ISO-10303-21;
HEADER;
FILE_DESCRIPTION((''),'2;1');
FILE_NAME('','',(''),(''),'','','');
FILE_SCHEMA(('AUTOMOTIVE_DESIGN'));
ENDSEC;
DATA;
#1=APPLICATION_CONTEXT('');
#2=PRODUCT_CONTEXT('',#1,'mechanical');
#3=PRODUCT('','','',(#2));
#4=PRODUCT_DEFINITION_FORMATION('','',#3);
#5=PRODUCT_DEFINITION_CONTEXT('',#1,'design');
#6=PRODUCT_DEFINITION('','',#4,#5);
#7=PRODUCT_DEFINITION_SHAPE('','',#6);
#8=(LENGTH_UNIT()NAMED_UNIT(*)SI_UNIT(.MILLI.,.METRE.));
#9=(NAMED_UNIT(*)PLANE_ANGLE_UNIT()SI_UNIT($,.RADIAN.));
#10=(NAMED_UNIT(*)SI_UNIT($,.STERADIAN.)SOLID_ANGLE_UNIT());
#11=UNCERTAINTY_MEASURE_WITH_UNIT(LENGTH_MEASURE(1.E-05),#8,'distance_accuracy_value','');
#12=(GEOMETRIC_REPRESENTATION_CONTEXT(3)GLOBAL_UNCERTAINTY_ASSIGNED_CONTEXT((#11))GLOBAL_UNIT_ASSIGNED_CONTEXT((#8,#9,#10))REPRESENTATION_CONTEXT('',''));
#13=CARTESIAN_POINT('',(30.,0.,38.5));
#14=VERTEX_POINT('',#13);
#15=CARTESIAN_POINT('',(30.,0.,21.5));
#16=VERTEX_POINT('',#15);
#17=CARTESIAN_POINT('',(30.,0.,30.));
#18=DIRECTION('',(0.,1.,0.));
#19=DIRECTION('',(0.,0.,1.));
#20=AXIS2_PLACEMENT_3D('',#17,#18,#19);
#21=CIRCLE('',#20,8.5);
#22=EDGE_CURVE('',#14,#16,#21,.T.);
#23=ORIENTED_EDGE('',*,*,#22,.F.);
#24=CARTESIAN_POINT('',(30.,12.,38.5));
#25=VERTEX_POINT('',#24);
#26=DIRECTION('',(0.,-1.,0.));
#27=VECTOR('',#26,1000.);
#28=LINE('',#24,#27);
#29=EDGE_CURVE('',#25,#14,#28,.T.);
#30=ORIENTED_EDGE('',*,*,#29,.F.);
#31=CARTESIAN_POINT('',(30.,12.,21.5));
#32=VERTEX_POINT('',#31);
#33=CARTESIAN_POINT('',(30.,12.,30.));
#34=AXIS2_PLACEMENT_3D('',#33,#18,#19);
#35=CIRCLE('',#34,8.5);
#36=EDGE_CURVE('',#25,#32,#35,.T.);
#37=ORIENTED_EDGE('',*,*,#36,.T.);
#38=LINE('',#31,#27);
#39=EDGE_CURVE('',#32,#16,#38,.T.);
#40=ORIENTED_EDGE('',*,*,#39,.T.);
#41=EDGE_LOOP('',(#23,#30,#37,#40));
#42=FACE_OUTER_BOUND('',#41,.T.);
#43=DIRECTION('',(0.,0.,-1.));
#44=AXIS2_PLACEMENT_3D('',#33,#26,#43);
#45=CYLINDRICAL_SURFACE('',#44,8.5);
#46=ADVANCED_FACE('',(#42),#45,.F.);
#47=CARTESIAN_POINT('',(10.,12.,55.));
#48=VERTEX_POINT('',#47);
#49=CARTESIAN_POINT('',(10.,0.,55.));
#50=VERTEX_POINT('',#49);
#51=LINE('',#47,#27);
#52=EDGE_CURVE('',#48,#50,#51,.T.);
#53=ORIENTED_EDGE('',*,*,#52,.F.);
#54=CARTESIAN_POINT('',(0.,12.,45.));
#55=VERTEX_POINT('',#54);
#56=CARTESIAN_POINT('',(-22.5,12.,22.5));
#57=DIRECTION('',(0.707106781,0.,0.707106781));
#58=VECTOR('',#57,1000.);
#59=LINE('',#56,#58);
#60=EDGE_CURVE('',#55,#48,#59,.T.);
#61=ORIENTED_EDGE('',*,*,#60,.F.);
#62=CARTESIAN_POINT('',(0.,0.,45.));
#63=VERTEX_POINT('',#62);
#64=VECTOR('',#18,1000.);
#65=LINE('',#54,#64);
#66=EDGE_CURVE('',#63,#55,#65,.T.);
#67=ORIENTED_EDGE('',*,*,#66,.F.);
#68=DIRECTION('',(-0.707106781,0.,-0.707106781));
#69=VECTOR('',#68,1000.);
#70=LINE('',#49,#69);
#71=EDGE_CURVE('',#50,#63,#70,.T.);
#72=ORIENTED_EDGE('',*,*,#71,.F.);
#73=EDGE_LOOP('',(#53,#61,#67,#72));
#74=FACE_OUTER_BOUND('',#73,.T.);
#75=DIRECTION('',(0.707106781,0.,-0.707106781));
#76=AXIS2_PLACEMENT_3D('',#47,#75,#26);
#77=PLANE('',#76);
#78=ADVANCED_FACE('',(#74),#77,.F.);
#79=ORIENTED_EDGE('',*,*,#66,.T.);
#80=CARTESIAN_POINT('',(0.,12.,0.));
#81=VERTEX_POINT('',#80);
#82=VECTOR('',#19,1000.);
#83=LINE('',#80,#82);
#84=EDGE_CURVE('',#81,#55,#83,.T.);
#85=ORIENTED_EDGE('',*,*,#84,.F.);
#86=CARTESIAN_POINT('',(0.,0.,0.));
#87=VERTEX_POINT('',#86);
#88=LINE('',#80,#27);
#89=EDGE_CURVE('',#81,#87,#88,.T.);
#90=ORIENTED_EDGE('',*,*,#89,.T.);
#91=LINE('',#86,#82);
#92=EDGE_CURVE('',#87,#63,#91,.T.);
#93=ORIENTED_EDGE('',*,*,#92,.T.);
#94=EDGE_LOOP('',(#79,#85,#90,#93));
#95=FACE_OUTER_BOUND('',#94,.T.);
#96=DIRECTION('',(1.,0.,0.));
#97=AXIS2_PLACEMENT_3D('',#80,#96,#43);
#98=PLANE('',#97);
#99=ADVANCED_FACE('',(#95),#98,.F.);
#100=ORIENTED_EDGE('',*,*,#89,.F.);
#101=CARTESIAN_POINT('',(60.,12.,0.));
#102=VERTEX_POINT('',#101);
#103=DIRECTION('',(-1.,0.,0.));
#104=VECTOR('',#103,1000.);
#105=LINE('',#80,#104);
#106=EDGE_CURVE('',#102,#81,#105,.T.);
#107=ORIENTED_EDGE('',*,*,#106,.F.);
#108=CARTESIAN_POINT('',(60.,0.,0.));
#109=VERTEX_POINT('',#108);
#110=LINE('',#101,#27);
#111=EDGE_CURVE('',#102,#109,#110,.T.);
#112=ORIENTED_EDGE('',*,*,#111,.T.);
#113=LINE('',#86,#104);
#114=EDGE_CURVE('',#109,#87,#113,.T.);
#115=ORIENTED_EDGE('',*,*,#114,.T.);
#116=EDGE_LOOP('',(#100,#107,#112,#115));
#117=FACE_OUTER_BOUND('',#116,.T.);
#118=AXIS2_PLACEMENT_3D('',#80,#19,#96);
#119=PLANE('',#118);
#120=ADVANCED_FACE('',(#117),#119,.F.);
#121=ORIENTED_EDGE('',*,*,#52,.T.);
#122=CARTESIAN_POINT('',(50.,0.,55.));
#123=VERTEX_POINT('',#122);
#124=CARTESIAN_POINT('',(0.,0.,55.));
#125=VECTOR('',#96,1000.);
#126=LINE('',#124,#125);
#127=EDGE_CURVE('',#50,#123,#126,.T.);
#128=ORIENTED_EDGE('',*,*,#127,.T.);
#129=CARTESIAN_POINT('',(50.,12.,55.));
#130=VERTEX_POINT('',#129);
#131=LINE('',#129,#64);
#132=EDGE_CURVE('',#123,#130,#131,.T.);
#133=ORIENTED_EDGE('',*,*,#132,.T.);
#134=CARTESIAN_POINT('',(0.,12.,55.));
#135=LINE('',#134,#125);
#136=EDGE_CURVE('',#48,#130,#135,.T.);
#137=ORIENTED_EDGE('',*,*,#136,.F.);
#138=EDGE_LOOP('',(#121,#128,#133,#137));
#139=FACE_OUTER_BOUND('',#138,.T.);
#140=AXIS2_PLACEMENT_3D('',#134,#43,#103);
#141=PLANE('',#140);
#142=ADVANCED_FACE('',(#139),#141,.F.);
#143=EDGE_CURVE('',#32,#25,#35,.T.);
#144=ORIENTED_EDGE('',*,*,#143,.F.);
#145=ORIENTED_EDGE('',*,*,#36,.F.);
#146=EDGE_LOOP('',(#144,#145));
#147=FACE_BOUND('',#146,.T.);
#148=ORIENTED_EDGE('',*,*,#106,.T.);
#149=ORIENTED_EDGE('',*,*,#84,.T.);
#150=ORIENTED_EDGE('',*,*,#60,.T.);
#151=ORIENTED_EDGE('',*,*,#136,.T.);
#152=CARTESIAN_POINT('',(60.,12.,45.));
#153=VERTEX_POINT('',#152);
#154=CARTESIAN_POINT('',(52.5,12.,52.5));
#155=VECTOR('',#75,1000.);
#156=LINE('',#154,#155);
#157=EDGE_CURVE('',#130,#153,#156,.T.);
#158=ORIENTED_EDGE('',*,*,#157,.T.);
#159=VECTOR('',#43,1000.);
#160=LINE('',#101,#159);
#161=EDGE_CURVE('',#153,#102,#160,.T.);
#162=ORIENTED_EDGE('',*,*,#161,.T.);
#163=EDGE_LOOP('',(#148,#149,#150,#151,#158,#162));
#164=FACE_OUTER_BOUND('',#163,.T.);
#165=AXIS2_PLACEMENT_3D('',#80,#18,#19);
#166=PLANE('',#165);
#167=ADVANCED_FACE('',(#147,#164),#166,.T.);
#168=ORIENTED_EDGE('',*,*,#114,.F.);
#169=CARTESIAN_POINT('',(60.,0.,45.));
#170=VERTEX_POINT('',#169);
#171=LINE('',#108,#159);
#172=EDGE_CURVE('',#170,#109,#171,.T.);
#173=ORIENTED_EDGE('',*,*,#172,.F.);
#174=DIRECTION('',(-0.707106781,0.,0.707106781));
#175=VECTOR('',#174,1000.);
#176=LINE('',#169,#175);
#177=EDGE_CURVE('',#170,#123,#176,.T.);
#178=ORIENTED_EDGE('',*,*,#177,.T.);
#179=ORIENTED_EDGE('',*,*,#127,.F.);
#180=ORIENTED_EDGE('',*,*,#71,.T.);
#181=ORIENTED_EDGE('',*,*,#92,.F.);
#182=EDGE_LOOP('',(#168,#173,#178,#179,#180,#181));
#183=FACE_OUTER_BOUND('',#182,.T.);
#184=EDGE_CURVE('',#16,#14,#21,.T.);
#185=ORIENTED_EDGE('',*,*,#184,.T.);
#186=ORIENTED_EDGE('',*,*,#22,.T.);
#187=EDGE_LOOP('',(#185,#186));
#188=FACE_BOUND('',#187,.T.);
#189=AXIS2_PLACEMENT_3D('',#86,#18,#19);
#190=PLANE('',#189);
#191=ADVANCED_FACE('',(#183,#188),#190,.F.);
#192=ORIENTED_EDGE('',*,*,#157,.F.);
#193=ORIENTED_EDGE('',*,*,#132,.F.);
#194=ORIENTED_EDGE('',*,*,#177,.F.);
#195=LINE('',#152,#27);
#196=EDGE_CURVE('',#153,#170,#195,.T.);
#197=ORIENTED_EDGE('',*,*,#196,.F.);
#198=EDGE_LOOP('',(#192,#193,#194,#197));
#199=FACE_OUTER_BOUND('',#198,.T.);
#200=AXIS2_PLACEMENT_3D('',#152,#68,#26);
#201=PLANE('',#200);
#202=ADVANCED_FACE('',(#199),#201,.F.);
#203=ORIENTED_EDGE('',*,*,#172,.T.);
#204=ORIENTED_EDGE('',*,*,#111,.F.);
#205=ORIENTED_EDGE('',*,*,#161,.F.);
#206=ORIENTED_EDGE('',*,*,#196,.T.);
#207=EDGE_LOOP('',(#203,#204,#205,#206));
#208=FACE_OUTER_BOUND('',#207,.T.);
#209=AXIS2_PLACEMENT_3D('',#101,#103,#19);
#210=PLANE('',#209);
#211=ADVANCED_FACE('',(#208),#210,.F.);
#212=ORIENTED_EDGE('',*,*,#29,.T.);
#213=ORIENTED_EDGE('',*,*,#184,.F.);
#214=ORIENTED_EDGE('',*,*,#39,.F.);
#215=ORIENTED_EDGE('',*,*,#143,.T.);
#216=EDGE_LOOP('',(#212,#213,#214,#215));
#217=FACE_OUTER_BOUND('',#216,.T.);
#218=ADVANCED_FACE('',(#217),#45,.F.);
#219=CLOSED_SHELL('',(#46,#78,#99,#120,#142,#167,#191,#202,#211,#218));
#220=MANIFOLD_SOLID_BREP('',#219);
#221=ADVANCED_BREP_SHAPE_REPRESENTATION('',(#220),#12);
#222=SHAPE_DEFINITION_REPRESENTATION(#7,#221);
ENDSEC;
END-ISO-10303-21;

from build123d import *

# Parameters (mm, degrees)
SKETCH1_W           = 60
SKETCH1_H           = 55
SKETCH1_R           = 8.5
BOSS_EXTRUDE1_DEPTH = 12
CHAMFER1_SIZE       = 10


with BuildPart() as part:
    # Sketch1 → Boss-Extrude1 (new body)
    with BuildSketch(Plane(origin=(0, 0, 0), x_dir=(1, 0, 0), z_dir=(0, 1, 0))):
        with Locations((30, -27.5)):
            Rectangle(SKETCH1_W, SKETCH1_H)
        with Locations(Location((30, -30, 0), (0, 0, 270))):
            Circle(SKETCH1_R, mode=Mode.SUBTRACT)
    extrude(amount=BOSS_EXTRUDE1_DEPTH)

    # Chamfer1
    chamfer1_edges = [part.edges().sort_by_distance(p)[0] for p in [
        (60, 6, 55),
        (0, 6, 55),
    ]]
    chamfer(chamfer1_edges, length=CHAMFER1_SIZE)


solid = part.part
